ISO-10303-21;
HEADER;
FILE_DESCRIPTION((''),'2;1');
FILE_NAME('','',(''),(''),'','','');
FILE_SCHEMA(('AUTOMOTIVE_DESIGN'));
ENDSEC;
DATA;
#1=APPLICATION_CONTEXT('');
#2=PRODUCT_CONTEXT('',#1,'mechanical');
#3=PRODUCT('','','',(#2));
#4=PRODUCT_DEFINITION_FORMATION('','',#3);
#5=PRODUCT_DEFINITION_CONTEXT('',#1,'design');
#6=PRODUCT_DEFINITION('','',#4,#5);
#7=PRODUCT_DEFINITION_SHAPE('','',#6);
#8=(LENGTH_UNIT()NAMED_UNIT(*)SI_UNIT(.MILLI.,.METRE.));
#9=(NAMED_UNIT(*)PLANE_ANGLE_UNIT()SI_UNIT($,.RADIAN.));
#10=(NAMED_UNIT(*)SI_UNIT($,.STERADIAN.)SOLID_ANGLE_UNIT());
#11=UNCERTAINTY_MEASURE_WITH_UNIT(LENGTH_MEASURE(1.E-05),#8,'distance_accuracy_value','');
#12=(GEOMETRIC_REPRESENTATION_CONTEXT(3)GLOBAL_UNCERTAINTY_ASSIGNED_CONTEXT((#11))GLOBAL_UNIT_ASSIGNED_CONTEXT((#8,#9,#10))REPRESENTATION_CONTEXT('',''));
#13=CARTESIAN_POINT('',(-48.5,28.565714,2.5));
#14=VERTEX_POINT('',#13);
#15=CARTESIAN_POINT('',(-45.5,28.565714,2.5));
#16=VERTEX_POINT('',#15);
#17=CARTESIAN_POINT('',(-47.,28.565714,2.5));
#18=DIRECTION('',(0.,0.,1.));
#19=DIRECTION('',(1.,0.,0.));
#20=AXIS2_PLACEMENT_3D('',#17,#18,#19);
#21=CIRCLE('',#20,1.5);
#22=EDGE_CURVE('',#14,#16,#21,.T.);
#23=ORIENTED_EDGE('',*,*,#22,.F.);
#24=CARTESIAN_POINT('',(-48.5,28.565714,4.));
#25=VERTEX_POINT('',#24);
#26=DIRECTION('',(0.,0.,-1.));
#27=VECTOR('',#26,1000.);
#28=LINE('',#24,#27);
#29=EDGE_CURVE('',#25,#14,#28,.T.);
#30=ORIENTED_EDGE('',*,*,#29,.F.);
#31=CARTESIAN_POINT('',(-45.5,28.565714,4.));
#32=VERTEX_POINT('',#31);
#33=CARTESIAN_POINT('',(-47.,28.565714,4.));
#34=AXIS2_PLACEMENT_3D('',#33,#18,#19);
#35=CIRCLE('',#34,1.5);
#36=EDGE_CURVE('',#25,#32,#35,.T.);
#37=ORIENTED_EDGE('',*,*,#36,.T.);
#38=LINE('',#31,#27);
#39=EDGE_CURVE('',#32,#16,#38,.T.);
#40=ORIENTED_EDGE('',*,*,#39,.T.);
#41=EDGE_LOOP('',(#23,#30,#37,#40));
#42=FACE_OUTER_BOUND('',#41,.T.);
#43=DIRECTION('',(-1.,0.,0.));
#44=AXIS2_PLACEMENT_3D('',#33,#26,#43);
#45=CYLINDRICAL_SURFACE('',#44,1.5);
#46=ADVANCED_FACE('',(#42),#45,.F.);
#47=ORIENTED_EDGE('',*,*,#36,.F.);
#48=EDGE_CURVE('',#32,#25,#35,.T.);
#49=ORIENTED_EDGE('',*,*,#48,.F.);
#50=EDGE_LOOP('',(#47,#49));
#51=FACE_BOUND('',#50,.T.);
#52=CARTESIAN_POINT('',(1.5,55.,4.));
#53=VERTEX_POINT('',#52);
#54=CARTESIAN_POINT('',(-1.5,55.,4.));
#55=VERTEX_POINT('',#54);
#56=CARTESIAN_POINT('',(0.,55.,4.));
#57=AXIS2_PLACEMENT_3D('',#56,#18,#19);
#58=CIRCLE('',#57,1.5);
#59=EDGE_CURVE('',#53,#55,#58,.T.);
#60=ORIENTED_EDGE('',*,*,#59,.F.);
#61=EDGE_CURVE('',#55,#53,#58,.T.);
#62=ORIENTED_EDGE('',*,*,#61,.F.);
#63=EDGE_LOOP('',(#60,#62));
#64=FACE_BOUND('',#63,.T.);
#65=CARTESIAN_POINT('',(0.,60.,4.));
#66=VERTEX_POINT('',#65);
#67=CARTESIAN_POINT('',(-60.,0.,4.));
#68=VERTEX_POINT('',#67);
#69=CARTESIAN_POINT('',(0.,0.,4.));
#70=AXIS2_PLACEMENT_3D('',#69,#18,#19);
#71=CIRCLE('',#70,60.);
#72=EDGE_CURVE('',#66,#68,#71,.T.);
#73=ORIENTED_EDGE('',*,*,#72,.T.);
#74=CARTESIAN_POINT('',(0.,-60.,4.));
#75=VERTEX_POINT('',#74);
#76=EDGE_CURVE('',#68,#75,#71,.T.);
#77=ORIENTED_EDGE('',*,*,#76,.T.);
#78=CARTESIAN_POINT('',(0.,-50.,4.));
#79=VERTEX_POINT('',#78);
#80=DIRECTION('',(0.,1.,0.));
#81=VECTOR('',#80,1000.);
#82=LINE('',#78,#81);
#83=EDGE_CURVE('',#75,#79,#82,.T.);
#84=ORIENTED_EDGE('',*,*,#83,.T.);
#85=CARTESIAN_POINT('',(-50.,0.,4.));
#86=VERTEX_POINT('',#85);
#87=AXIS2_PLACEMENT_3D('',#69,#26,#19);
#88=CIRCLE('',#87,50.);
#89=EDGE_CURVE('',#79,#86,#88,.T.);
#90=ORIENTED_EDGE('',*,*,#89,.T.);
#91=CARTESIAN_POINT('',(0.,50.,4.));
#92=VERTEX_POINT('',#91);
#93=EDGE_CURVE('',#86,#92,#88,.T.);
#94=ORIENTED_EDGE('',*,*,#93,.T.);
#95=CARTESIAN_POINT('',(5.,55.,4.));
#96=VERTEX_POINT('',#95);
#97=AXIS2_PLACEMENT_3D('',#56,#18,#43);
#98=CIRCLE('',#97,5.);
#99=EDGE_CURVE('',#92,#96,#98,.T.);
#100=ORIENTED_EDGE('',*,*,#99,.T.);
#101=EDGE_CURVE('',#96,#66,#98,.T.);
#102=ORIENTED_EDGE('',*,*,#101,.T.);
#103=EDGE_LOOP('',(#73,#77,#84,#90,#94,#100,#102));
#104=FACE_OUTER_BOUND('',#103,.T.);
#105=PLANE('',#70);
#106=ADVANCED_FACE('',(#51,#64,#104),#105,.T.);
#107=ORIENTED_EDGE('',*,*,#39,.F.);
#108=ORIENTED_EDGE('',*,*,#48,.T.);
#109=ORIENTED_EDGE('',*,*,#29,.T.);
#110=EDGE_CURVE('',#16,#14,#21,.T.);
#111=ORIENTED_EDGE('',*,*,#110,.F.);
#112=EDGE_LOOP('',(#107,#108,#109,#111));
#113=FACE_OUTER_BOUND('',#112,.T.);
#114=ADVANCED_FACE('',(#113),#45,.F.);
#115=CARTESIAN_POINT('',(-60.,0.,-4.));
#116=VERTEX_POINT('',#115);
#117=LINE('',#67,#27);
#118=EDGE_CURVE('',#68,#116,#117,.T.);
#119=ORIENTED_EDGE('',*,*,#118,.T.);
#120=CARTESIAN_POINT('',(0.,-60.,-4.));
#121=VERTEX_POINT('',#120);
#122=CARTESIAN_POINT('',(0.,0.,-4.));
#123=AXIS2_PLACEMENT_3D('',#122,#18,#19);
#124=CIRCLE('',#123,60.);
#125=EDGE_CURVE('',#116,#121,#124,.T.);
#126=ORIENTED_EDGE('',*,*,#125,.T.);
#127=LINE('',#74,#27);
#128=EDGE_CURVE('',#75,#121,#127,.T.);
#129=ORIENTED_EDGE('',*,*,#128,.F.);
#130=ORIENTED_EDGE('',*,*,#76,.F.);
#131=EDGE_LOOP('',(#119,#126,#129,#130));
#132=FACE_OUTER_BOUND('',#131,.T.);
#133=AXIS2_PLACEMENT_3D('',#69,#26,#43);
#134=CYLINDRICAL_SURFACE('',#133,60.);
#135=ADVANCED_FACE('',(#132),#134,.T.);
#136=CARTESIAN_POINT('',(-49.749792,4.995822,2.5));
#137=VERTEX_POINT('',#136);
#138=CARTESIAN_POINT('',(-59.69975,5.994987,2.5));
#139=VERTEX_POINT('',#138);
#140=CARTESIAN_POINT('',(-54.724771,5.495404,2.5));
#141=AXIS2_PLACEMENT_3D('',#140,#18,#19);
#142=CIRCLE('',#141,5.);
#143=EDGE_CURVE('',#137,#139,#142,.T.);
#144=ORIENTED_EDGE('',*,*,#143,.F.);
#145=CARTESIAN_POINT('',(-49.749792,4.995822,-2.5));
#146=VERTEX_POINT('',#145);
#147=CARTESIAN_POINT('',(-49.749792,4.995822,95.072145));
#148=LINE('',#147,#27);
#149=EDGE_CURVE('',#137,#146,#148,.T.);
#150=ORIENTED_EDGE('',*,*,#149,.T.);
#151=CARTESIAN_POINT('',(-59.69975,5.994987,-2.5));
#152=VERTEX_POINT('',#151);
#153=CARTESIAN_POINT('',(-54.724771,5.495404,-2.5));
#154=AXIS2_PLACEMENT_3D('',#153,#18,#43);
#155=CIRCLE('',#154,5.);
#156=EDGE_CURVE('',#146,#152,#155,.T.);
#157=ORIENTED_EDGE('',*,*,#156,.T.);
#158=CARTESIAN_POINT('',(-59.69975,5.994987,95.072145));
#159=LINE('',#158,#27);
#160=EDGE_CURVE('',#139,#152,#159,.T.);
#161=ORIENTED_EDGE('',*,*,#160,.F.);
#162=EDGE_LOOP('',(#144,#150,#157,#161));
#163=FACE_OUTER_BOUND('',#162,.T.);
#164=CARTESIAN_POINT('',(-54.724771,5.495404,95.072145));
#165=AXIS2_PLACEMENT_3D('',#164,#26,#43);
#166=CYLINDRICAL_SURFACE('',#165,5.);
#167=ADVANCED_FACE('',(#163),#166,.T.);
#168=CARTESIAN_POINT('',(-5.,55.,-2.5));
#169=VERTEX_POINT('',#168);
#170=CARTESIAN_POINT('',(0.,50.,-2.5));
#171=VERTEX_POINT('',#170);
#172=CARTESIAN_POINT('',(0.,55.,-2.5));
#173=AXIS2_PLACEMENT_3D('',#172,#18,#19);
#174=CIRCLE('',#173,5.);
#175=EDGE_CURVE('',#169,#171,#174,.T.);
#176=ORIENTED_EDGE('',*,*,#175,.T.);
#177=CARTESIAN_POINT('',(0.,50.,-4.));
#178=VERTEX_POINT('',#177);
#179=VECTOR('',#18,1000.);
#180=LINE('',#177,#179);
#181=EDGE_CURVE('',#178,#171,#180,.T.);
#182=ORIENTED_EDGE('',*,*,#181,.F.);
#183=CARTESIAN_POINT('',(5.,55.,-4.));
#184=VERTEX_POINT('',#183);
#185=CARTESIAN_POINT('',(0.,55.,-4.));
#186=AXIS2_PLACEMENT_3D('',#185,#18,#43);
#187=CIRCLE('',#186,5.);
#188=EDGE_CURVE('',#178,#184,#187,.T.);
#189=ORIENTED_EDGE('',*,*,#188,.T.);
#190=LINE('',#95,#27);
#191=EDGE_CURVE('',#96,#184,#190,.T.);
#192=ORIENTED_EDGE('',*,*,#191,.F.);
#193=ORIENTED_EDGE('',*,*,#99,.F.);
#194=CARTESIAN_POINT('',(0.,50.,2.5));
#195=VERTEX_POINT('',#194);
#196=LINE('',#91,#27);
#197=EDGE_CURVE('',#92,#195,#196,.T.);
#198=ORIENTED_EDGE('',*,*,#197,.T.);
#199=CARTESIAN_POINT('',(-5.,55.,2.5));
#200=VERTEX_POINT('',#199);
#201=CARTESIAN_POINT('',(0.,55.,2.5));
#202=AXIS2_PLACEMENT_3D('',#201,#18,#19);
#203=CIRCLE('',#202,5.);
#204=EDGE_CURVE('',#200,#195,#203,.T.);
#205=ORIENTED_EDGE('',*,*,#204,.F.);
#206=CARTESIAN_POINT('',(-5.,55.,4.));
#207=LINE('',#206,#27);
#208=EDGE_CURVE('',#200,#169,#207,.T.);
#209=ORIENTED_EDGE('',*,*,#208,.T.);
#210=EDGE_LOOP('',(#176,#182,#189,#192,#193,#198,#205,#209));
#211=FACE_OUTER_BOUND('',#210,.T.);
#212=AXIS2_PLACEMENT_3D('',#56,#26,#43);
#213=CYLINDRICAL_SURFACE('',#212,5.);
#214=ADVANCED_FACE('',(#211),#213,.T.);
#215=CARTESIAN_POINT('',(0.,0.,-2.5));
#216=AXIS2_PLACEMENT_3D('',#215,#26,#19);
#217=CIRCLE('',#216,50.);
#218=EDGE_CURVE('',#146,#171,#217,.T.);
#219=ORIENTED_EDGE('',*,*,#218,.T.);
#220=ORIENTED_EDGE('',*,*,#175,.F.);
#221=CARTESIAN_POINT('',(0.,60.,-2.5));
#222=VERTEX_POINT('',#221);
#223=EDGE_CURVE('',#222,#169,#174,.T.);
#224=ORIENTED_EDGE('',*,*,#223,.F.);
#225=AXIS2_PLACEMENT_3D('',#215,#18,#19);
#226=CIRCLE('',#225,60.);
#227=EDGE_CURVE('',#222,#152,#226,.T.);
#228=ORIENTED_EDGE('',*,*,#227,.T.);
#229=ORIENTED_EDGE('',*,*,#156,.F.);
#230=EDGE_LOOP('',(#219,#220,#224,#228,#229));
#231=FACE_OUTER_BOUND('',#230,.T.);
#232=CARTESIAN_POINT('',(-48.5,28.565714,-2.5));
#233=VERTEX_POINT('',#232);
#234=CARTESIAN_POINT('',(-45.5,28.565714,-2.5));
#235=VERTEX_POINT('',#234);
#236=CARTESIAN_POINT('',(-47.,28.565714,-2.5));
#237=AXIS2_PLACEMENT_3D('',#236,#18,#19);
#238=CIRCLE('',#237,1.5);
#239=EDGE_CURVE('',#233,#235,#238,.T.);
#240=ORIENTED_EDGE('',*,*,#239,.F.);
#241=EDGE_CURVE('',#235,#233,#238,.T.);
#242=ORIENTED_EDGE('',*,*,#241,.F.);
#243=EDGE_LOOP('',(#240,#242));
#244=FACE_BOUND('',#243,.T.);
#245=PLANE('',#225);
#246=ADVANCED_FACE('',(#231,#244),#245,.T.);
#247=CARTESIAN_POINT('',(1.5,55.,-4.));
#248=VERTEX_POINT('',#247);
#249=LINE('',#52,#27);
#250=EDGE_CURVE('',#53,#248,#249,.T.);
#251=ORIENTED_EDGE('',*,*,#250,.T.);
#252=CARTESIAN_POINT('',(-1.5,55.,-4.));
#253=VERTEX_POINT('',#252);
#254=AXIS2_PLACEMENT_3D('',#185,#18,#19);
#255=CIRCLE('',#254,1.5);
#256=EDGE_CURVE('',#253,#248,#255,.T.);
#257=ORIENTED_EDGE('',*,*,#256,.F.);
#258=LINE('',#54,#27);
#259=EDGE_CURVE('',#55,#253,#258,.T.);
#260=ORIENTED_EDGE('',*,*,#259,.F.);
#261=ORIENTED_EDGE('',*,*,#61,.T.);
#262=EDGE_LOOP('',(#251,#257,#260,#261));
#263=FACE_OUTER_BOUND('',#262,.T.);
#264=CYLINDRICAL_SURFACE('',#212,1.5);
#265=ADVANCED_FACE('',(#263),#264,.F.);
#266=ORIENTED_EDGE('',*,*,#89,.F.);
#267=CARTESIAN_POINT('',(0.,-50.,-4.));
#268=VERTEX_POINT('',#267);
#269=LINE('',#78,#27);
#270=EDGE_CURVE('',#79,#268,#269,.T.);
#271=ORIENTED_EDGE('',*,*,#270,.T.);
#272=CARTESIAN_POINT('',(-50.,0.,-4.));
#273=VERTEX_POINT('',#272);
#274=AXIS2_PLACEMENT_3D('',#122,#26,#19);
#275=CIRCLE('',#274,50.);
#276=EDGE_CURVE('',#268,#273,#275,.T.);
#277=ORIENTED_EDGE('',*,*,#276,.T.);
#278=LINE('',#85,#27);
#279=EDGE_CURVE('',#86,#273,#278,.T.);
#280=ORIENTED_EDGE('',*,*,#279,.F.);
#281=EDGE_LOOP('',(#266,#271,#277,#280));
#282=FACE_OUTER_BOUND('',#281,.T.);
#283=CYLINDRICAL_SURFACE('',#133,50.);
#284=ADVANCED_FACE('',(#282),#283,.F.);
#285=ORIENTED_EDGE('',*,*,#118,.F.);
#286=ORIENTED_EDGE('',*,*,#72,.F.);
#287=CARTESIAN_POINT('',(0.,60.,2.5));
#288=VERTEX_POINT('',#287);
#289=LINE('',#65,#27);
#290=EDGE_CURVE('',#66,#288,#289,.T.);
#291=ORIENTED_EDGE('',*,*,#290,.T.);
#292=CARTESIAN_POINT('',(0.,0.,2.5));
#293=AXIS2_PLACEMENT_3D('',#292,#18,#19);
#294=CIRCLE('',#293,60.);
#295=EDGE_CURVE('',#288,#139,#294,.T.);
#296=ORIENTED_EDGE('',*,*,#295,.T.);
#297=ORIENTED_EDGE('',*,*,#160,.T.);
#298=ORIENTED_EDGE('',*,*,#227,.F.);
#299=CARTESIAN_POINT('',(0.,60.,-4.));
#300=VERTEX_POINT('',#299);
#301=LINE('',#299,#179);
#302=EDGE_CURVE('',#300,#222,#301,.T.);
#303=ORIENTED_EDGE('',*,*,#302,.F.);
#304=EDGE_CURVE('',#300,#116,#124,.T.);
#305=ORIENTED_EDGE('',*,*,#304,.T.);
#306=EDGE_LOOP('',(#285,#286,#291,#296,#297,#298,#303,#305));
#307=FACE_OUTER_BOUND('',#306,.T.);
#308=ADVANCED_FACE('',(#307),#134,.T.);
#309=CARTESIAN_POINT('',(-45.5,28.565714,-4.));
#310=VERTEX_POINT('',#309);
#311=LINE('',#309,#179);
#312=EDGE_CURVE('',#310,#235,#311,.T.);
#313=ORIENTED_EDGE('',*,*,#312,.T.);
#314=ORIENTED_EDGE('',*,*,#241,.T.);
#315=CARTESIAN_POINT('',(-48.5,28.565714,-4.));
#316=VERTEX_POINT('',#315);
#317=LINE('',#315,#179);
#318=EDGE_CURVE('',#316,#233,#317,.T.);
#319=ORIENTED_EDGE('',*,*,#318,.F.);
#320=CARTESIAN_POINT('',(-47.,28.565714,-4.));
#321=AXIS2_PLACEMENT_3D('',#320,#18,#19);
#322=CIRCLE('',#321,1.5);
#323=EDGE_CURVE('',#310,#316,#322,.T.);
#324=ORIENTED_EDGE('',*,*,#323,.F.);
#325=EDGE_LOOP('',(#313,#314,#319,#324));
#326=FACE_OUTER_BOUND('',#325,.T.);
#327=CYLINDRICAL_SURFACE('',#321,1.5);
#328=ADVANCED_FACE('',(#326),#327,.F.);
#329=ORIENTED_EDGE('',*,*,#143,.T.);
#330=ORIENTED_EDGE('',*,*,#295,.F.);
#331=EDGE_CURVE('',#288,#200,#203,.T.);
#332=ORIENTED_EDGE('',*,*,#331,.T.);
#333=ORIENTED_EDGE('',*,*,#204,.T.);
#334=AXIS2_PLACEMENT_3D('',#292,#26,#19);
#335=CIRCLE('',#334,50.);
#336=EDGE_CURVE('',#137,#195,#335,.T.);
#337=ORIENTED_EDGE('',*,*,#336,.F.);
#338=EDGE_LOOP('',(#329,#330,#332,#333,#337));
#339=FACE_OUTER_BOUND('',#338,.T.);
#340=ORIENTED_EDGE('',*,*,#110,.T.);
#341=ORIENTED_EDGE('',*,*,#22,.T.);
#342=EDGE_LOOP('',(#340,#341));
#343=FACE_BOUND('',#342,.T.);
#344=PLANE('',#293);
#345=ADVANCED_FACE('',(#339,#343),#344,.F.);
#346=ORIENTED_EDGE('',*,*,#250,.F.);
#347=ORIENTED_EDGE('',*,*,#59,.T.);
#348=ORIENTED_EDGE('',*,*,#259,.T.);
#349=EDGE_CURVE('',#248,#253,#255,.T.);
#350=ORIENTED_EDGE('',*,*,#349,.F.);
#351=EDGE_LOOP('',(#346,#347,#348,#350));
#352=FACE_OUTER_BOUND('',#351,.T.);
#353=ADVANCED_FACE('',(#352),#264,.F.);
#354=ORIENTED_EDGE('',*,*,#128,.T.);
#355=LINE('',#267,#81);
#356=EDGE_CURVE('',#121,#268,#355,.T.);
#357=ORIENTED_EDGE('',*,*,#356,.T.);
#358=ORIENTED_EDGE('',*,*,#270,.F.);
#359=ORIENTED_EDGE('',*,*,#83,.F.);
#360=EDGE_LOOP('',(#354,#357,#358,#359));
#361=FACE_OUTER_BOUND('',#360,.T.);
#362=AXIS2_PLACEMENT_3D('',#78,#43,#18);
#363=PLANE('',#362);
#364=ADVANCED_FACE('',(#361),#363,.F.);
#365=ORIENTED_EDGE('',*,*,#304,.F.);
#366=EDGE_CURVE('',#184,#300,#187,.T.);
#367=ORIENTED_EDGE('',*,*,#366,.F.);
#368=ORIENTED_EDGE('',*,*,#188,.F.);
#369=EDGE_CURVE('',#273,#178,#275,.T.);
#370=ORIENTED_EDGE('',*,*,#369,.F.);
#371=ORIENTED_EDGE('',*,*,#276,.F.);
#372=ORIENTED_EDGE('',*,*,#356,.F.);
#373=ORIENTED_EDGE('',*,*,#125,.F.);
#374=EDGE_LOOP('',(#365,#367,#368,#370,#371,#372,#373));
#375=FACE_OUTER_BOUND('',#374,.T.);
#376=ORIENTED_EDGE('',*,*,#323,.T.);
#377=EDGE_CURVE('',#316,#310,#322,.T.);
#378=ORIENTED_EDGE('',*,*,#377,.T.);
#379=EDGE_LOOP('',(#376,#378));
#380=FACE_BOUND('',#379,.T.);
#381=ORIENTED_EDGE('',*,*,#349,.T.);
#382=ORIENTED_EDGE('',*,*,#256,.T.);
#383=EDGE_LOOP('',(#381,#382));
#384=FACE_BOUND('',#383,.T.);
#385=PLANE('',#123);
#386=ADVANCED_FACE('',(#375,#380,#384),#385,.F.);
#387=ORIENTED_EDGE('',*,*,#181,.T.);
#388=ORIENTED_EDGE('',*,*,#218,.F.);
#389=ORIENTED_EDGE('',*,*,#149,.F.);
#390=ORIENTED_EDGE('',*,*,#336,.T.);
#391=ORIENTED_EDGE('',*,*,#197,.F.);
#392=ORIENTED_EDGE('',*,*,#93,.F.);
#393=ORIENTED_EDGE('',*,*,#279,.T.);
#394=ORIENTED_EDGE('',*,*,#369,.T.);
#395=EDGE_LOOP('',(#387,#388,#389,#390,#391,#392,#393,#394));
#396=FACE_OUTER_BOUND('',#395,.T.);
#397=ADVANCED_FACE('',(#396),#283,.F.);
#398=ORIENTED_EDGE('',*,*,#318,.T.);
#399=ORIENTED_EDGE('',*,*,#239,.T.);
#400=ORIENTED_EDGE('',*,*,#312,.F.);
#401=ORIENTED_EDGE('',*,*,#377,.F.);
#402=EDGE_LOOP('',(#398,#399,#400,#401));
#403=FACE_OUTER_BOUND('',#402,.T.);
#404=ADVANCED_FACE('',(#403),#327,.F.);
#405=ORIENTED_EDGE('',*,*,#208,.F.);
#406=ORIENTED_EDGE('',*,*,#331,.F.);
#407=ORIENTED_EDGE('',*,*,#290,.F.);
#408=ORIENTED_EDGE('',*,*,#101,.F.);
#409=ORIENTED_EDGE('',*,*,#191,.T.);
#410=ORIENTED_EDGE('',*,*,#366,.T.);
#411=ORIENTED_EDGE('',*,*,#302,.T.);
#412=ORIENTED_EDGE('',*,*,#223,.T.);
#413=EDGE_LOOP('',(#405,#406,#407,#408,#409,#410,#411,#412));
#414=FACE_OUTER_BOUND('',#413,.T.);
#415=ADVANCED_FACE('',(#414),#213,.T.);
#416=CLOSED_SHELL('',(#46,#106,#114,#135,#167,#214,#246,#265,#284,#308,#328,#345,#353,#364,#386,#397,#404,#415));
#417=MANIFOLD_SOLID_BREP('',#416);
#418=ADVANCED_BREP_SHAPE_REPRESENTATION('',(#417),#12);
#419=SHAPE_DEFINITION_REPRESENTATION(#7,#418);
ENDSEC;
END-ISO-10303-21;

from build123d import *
from build123d.topology import SkipClean

# Parameters (mm, degrees)
FRONT_START                = 2.5
ARC_ARM_PROFILE_SKETCH_R   = 1.5
FRONT_ARC_PLATE_DEPTH      = 1.5
REAR_START                 = -2.5
SKETCH1_2_R                = 1.5
REAR_ARC_PLATE_DEPTH       = 1.5
END_SPACER_SKETCH_R        = 5
END_SPACER_SKETCH_R_2      = 1.5
END_SPACER_BLOCK_5MM_DEPTH = 5


with BuildPart() as part:
    # Arc Arm Profile Sketch → Front Arc Plate (new body)
    with BuildSketch(Plane.XY.offset(FRONT_START)):
        with BuildLine():
            Line((0, -50), (0, -60))
            ThreePointArc((0, -60), (-60, 0), (0, 60))
            ThreePointArc((0, 60), (5, 55), (0, 50))
            ThreePointArc((0, 50), (-50, 0), (0, -50))
        make_face()
        with Locations((0, 55)):
            Circle(ARC_ARM_PROFILE_SKETCH_R, mode=Mode.SUBTRACT)
        with Locations((-47, 28.565713714)):
            Circle(ARC_ARM_PROFILE_SKETCH_R, mode=Mode.SUBTRACT)
    extrude(amount=FRONT_ARC_PLATE_DEPTH)



with BuildPart() as body_2:
    # Sketch1_2 → Rear Arc Plate (new body)
    with BuildSketch(Plane.XY.offset(REAR_START)):
        with BuildLine():
            Line((0, -50), (0, -60))
            ThreePointArc((0, -60), (-60, 0), (0, 60))
            ThreePointArc((0, 60), (5, 55), (0, 50))
            ThreePointArc((0, 50), (-50, 0), (0, -50))
        make_face()
        with Locations((0, 55)):
            Circle(SKETCH1_2_R, mode=Mode.SUBTRACT)
        with Locations((-47, 28.565713714)):
            Circle(SKETCH1_2_R, mode=Mode.SUBTRACT)
    extrude(amount=-REAR_ARC_PLATE_DEPTH)


with BuildPart() as part_1:
    with SkipClean():  # the faces are left unmerged after this step: merging them gives an invalid solid
        add(part.part)

        add(body_2.part)  # End Spacer Block 5mm merges body 2
        # End Spacer Sketch → End Spacer Block 5mm (add)
        # profile 1 of 2: a face of its own
        with BuildSketch(Plane.XY.offset(-2.5)):
            with Locations(Location((0, 55, 0), (0, 0, 270))):
                Circle(END_SPACER_SKETCH_R)
            with Locations((0, 55)):
                Circle(END_SPACER_SKETCH_R_2, mode=Mode.SUBTRACT)
        # profile 2 of 2: a face of its own
        with BuildSketch(Plane.XY.offset(-2.5)):
            with BuildLine():
                Line((0, -60), (0, -50))
                ThreePointArc((0, -50), (-37.079584068, -33.542576606), (-49.749791564, 4.995822185))
                ThreePointArc((-49.749791564, 4.995822185), (-54.225188502, 10.47038356), (-59.699749877, 5.994986622))
                ThreePointArc((-59.699749877, 5.994986622), (-44.495500881, -40.251091927), (0, -60))
            make_face()
        extrude(amount=END_SPACER_BLOCK_5MM_DEPTH)


solid = part_1.part
